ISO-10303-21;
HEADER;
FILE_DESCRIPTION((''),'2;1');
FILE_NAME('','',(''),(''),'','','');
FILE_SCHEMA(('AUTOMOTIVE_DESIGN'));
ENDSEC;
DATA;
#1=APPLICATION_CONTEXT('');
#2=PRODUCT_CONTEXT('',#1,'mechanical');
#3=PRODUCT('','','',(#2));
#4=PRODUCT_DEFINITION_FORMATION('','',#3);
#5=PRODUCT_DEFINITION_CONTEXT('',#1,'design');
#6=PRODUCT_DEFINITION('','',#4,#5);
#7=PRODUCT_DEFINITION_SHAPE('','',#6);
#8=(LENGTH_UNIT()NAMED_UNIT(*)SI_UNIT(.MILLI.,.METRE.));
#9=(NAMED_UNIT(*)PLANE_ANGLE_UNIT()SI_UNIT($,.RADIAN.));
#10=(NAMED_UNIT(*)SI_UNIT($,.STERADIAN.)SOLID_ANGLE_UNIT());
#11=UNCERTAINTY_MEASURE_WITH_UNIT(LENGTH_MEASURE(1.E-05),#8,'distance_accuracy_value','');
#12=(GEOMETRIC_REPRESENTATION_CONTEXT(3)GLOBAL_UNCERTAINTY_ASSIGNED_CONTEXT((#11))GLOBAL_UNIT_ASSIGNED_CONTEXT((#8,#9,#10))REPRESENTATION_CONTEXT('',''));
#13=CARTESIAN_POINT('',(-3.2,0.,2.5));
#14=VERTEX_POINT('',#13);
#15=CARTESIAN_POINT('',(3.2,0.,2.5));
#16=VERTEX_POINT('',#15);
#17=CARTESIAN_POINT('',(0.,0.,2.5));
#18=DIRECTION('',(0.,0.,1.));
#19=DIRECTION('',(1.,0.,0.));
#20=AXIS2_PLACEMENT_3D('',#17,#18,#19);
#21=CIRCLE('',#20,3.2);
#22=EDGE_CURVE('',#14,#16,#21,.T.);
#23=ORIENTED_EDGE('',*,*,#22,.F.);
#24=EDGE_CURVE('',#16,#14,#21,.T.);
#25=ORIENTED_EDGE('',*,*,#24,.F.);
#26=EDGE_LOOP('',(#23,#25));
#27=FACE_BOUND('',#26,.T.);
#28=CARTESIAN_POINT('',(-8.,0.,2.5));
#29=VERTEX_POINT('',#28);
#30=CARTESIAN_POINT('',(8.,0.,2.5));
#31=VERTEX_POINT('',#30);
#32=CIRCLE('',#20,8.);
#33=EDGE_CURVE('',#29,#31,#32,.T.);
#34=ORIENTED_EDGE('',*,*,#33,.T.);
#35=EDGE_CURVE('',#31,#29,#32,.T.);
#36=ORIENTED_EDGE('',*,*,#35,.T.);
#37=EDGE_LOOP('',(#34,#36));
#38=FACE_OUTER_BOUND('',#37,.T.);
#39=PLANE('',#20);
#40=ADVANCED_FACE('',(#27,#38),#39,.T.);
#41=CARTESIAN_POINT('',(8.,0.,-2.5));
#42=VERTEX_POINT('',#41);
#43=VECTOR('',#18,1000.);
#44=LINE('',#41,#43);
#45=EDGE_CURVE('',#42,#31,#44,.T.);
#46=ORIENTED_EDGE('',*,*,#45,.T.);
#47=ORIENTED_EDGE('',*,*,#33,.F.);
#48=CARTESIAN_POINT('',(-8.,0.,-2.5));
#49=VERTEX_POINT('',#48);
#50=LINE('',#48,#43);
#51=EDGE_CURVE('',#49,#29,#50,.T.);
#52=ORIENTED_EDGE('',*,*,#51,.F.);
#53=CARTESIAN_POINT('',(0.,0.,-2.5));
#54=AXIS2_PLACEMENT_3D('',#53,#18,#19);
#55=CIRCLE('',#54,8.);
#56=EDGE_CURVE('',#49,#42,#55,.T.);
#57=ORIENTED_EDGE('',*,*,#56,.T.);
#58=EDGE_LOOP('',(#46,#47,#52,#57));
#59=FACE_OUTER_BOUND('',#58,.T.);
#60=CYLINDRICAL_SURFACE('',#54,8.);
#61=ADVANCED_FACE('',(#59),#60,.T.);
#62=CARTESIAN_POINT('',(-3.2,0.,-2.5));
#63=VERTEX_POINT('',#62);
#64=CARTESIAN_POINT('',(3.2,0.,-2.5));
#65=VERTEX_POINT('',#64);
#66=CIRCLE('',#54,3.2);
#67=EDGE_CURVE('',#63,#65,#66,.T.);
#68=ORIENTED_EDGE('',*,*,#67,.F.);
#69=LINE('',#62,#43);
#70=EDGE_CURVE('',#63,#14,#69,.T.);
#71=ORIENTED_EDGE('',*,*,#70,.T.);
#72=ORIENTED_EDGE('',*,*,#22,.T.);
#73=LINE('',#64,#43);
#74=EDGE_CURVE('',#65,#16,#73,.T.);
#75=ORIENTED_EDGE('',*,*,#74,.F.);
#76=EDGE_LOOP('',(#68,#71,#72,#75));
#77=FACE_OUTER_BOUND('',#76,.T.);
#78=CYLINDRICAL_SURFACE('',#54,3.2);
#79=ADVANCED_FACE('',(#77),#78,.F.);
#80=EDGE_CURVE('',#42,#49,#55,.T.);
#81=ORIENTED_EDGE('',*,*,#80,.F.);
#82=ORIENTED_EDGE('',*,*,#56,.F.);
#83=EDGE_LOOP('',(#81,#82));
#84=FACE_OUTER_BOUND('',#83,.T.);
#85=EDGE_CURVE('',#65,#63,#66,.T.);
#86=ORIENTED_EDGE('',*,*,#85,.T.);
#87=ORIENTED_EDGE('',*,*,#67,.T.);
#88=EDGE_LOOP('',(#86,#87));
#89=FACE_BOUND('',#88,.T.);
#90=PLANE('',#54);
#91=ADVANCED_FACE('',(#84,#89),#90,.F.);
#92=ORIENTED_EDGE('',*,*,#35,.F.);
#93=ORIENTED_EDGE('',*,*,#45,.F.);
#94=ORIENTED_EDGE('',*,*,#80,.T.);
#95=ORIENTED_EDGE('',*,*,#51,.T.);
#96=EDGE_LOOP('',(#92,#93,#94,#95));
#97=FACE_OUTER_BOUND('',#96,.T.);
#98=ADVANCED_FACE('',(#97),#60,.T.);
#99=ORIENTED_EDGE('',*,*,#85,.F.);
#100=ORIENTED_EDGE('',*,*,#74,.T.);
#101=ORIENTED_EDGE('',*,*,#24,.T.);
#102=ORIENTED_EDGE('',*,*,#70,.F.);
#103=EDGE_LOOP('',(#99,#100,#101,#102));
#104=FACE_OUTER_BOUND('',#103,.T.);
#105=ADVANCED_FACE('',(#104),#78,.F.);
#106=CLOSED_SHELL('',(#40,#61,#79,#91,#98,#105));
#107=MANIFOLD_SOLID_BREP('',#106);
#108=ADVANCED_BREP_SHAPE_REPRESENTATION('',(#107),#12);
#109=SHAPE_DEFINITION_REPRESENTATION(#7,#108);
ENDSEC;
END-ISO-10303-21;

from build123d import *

# Parameters (mm, degrees)
SKETCH_1_R      = 8
SKETCH_1_R_2    = 3.2
EXTRUDE_1_DEPTH = 2.5


with BuildPart() as part:
    # 草图1 → 凸台-拉伸1 (new, symmetric)
    with BuildSketch(Plane.XY):
        Circle(SKETCH_1_R)
        Circle(SKETCH_1_R_2, mode=Mode.SUBTRACT)
    extrude(amount=EXTRUDE_1_DEPTH, both=True)


solid = part.part
